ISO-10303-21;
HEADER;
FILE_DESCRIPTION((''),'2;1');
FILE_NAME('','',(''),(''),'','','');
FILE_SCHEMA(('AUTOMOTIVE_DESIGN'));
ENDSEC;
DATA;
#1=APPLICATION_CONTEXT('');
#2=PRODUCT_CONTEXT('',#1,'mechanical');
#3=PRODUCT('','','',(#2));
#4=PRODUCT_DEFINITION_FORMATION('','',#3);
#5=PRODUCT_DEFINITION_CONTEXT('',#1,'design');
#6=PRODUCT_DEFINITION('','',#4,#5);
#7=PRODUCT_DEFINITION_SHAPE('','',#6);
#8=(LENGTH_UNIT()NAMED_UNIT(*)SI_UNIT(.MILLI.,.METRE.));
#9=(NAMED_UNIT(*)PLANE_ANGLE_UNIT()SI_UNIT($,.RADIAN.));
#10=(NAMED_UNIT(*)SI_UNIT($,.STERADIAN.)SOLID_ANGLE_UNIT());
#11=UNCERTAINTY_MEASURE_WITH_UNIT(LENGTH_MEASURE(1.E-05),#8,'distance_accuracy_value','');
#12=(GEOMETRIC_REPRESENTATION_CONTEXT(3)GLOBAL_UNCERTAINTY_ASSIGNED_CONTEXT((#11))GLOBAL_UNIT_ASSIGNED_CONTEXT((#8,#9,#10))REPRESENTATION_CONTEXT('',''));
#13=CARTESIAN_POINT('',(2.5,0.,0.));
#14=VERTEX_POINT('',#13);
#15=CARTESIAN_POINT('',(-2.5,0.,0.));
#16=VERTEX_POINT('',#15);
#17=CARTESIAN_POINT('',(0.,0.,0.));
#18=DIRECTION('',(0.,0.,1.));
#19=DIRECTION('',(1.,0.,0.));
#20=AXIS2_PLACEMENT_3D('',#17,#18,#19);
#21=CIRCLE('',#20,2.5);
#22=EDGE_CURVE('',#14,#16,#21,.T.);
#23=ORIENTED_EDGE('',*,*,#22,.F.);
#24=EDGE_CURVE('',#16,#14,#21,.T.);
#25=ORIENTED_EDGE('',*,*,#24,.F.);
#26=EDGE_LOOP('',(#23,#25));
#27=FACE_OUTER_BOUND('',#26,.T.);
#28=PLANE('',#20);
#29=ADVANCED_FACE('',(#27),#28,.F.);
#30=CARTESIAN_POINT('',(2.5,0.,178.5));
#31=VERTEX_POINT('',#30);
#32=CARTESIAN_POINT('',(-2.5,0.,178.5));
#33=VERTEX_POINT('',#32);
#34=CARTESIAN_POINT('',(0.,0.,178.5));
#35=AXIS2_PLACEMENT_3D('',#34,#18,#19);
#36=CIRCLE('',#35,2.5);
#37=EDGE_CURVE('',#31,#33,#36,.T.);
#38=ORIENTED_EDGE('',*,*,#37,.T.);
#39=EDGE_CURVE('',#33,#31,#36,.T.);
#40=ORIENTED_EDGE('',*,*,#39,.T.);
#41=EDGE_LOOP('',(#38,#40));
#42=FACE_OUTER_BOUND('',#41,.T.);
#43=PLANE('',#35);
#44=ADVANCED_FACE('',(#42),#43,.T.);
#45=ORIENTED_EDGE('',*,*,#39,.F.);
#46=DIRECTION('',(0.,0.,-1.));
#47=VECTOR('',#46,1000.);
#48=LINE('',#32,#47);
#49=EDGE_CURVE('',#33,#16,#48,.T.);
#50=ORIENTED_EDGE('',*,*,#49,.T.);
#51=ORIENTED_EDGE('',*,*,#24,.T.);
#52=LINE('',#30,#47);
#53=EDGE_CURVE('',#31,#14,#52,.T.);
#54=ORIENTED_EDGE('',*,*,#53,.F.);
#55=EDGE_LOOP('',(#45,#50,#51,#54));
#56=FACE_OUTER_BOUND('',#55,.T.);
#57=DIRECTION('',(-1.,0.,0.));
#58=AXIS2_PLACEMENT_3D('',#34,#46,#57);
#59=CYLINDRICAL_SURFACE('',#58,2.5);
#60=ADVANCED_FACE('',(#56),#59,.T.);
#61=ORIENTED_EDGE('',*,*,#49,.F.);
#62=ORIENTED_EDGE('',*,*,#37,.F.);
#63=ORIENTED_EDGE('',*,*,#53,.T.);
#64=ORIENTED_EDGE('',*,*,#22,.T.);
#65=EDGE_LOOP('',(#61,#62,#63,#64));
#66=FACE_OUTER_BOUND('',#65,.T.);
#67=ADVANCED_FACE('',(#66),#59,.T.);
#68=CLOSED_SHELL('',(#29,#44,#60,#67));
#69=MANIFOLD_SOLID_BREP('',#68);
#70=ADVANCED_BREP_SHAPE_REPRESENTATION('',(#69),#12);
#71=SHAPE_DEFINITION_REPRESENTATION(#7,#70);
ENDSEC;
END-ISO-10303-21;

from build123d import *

# Parameters (mm, degrees)
SKETCH1_R           = 2.5
BOSS_EXTRUDE1_DEPTH = 178.5


with BuildPart() as part:
    # Sketch1 → Boss-Extrude1 (new body)
    with BuildSketch(Plane.XY):
        Circle(SKETCH1_R)
    extrude(amount=BOSS_EXTRUDE1_DEPTH)


solid = part.part
